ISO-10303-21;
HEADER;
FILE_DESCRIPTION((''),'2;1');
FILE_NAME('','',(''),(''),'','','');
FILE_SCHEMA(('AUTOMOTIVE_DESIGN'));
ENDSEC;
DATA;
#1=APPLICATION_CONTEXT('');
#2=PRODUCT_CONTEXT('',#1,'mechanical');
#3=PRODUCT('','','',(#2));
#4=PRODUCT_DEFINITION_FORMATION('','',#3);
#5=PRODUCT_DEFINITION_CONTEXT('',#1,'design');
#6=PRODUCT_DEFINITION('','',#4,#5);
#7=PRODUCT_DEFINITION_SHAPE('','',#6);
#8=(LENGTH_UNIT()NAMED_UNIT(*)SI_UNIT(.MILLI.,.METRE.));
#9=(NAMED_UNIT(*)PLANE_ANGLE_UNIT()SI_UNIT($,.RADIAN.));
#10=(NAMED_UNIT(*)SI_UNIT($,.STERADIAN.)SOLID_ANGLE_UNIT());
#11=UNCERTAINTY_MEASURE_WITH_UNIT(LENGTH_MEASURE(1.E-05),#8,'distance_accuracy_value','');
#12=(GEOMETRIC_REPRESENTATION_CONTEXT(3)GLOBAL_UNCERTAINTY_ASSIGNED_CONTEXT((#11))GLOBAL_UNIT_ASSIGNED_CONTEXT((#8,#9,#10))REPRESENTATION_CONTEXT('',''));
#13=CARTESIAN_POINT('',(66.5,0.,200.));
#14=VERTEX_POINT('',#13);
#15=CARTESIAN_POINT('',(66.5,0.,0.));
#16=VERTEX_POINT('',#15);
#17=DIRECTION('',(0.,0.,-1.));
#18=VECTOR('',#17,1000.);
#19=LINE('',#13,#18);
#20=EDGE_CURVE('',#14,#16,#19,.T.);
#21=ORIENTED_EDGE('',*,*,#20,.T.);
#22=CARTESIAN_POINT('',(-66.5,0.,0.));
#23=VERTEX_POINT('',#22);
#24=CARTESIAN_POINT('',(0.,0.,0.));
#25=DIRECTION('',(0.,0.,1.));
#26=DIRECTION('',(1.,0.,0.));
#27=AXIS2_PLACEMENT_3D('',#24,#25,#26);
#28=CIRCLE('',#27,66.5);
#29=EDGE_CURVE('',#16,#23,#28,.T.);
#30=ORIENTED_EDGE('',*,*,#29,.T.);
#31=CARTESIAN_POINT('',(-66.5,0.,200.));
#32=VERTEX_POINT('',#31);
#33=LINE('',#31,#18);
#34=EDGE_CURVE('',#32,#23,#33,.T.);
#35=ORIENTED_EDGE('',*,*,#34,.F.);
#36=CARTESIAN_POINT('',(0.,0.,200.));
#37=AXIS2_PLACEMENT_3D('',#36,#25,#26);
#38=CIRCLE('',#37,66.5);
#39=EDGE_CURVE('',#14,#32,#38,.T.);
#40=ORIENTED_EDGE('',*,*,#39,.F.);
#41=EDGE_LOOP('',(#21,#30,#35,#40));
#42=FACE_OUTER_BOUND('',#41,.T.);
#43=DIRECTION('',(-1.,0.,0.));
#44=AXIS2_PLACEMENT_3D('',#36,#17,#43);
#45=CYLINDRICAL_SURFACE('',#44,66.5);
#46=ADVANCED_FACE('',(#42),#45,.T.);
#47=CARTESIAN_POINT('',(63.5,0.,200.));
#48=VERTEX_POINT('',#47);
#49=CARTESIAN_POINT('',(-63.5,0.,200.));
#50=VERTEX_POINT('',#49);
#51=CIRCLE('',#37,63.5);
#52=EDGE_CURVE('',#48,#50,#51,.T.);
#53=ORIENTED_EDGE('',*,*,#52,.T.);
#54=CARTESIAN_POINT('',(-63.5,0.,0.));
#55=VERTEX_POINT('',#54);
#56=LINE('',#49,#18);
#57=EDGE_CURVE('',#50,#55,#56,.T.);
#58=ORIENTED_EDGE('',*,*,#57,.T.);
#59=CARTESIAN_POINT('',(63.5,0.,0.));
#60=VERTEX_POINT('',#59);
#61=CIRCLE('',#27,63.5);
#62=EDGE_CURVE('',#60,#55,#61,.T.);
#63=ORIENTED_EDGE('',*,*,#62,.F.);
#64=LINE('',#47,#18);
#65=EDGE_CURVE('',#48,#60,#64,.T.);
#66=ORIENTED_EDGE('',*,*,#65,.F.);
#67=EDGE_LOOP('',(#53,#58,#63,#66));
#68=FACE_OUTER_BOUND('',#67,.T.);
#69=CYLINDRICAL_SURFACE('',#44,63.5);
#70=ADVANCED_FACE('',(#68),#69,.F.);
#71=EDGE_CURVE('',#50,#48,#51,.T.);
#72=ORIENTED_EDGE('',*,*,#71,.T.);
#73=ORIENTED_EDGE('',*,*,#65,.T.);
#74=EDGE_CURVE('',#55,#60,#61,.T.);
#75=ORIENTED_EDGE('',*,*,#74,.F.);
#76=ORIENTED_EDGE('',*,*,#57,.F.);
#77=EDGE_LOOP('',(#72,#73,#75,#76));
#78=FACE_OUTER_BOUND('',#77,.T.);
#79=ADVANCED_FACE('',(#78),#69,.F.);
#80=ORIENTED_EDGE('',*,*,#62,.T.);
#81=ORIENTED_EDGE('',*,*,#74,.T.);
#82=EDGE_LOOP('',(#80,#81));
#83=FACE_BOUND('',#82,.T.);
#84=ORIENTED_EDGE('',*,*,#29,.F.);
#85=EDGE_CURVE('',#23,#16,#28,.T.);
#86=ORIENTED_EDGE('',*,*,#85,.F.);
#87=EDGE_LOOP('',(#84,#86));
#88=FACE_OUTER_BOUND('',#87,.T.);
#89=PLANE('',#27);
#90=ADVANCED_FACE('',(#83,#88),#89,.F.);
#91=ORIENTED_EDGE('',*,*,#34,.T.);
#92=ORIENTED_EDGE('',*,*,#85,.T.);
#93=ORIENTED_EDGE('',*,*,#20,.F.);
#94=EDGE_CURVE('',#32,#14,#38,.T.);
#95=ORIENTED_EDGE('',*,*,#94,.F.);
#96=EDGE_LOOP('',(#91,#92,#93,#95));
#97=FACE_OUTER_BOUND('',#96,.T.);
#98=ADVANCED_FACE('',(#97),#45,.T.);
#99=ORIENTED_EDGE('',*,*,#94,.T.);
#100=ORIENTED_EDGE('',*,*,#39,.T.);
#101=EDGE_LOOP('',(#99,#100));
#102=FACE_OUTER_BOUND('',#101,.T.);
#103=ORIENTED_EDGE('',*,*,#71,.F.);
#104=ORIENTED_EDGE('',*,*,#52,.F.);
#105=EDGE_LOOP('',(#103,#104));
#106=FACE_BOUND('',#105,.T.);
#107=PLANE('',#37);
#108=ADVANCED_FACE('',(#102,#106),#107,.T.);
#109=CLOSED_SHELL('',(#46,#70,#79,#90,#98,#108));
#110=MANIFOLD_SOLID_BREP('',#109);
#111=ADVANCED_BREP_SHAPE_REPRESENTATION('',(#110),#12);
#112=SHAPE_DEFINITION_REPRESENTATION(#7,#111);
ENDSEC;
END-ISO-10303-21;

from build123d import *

# Parameters (mm, degrees)
SKETCH1_R           = 66.5
SKETCH1_R_2         = 63.5
BOSS_EXTRUDE1_DEPTH = 200


with BuildPart() as part:
    # Sketch1 → Boss-Extrude1 (new body)
    with BuildSketch(Plane.XY):
        Circle(SKETCH1_R)
        Circle(SKETCH1_R_2, mode=Mode.SUBTRACT)
    extrude(amount=BOSS_EXTRUDE1_DEPTH)


solid = part.part
